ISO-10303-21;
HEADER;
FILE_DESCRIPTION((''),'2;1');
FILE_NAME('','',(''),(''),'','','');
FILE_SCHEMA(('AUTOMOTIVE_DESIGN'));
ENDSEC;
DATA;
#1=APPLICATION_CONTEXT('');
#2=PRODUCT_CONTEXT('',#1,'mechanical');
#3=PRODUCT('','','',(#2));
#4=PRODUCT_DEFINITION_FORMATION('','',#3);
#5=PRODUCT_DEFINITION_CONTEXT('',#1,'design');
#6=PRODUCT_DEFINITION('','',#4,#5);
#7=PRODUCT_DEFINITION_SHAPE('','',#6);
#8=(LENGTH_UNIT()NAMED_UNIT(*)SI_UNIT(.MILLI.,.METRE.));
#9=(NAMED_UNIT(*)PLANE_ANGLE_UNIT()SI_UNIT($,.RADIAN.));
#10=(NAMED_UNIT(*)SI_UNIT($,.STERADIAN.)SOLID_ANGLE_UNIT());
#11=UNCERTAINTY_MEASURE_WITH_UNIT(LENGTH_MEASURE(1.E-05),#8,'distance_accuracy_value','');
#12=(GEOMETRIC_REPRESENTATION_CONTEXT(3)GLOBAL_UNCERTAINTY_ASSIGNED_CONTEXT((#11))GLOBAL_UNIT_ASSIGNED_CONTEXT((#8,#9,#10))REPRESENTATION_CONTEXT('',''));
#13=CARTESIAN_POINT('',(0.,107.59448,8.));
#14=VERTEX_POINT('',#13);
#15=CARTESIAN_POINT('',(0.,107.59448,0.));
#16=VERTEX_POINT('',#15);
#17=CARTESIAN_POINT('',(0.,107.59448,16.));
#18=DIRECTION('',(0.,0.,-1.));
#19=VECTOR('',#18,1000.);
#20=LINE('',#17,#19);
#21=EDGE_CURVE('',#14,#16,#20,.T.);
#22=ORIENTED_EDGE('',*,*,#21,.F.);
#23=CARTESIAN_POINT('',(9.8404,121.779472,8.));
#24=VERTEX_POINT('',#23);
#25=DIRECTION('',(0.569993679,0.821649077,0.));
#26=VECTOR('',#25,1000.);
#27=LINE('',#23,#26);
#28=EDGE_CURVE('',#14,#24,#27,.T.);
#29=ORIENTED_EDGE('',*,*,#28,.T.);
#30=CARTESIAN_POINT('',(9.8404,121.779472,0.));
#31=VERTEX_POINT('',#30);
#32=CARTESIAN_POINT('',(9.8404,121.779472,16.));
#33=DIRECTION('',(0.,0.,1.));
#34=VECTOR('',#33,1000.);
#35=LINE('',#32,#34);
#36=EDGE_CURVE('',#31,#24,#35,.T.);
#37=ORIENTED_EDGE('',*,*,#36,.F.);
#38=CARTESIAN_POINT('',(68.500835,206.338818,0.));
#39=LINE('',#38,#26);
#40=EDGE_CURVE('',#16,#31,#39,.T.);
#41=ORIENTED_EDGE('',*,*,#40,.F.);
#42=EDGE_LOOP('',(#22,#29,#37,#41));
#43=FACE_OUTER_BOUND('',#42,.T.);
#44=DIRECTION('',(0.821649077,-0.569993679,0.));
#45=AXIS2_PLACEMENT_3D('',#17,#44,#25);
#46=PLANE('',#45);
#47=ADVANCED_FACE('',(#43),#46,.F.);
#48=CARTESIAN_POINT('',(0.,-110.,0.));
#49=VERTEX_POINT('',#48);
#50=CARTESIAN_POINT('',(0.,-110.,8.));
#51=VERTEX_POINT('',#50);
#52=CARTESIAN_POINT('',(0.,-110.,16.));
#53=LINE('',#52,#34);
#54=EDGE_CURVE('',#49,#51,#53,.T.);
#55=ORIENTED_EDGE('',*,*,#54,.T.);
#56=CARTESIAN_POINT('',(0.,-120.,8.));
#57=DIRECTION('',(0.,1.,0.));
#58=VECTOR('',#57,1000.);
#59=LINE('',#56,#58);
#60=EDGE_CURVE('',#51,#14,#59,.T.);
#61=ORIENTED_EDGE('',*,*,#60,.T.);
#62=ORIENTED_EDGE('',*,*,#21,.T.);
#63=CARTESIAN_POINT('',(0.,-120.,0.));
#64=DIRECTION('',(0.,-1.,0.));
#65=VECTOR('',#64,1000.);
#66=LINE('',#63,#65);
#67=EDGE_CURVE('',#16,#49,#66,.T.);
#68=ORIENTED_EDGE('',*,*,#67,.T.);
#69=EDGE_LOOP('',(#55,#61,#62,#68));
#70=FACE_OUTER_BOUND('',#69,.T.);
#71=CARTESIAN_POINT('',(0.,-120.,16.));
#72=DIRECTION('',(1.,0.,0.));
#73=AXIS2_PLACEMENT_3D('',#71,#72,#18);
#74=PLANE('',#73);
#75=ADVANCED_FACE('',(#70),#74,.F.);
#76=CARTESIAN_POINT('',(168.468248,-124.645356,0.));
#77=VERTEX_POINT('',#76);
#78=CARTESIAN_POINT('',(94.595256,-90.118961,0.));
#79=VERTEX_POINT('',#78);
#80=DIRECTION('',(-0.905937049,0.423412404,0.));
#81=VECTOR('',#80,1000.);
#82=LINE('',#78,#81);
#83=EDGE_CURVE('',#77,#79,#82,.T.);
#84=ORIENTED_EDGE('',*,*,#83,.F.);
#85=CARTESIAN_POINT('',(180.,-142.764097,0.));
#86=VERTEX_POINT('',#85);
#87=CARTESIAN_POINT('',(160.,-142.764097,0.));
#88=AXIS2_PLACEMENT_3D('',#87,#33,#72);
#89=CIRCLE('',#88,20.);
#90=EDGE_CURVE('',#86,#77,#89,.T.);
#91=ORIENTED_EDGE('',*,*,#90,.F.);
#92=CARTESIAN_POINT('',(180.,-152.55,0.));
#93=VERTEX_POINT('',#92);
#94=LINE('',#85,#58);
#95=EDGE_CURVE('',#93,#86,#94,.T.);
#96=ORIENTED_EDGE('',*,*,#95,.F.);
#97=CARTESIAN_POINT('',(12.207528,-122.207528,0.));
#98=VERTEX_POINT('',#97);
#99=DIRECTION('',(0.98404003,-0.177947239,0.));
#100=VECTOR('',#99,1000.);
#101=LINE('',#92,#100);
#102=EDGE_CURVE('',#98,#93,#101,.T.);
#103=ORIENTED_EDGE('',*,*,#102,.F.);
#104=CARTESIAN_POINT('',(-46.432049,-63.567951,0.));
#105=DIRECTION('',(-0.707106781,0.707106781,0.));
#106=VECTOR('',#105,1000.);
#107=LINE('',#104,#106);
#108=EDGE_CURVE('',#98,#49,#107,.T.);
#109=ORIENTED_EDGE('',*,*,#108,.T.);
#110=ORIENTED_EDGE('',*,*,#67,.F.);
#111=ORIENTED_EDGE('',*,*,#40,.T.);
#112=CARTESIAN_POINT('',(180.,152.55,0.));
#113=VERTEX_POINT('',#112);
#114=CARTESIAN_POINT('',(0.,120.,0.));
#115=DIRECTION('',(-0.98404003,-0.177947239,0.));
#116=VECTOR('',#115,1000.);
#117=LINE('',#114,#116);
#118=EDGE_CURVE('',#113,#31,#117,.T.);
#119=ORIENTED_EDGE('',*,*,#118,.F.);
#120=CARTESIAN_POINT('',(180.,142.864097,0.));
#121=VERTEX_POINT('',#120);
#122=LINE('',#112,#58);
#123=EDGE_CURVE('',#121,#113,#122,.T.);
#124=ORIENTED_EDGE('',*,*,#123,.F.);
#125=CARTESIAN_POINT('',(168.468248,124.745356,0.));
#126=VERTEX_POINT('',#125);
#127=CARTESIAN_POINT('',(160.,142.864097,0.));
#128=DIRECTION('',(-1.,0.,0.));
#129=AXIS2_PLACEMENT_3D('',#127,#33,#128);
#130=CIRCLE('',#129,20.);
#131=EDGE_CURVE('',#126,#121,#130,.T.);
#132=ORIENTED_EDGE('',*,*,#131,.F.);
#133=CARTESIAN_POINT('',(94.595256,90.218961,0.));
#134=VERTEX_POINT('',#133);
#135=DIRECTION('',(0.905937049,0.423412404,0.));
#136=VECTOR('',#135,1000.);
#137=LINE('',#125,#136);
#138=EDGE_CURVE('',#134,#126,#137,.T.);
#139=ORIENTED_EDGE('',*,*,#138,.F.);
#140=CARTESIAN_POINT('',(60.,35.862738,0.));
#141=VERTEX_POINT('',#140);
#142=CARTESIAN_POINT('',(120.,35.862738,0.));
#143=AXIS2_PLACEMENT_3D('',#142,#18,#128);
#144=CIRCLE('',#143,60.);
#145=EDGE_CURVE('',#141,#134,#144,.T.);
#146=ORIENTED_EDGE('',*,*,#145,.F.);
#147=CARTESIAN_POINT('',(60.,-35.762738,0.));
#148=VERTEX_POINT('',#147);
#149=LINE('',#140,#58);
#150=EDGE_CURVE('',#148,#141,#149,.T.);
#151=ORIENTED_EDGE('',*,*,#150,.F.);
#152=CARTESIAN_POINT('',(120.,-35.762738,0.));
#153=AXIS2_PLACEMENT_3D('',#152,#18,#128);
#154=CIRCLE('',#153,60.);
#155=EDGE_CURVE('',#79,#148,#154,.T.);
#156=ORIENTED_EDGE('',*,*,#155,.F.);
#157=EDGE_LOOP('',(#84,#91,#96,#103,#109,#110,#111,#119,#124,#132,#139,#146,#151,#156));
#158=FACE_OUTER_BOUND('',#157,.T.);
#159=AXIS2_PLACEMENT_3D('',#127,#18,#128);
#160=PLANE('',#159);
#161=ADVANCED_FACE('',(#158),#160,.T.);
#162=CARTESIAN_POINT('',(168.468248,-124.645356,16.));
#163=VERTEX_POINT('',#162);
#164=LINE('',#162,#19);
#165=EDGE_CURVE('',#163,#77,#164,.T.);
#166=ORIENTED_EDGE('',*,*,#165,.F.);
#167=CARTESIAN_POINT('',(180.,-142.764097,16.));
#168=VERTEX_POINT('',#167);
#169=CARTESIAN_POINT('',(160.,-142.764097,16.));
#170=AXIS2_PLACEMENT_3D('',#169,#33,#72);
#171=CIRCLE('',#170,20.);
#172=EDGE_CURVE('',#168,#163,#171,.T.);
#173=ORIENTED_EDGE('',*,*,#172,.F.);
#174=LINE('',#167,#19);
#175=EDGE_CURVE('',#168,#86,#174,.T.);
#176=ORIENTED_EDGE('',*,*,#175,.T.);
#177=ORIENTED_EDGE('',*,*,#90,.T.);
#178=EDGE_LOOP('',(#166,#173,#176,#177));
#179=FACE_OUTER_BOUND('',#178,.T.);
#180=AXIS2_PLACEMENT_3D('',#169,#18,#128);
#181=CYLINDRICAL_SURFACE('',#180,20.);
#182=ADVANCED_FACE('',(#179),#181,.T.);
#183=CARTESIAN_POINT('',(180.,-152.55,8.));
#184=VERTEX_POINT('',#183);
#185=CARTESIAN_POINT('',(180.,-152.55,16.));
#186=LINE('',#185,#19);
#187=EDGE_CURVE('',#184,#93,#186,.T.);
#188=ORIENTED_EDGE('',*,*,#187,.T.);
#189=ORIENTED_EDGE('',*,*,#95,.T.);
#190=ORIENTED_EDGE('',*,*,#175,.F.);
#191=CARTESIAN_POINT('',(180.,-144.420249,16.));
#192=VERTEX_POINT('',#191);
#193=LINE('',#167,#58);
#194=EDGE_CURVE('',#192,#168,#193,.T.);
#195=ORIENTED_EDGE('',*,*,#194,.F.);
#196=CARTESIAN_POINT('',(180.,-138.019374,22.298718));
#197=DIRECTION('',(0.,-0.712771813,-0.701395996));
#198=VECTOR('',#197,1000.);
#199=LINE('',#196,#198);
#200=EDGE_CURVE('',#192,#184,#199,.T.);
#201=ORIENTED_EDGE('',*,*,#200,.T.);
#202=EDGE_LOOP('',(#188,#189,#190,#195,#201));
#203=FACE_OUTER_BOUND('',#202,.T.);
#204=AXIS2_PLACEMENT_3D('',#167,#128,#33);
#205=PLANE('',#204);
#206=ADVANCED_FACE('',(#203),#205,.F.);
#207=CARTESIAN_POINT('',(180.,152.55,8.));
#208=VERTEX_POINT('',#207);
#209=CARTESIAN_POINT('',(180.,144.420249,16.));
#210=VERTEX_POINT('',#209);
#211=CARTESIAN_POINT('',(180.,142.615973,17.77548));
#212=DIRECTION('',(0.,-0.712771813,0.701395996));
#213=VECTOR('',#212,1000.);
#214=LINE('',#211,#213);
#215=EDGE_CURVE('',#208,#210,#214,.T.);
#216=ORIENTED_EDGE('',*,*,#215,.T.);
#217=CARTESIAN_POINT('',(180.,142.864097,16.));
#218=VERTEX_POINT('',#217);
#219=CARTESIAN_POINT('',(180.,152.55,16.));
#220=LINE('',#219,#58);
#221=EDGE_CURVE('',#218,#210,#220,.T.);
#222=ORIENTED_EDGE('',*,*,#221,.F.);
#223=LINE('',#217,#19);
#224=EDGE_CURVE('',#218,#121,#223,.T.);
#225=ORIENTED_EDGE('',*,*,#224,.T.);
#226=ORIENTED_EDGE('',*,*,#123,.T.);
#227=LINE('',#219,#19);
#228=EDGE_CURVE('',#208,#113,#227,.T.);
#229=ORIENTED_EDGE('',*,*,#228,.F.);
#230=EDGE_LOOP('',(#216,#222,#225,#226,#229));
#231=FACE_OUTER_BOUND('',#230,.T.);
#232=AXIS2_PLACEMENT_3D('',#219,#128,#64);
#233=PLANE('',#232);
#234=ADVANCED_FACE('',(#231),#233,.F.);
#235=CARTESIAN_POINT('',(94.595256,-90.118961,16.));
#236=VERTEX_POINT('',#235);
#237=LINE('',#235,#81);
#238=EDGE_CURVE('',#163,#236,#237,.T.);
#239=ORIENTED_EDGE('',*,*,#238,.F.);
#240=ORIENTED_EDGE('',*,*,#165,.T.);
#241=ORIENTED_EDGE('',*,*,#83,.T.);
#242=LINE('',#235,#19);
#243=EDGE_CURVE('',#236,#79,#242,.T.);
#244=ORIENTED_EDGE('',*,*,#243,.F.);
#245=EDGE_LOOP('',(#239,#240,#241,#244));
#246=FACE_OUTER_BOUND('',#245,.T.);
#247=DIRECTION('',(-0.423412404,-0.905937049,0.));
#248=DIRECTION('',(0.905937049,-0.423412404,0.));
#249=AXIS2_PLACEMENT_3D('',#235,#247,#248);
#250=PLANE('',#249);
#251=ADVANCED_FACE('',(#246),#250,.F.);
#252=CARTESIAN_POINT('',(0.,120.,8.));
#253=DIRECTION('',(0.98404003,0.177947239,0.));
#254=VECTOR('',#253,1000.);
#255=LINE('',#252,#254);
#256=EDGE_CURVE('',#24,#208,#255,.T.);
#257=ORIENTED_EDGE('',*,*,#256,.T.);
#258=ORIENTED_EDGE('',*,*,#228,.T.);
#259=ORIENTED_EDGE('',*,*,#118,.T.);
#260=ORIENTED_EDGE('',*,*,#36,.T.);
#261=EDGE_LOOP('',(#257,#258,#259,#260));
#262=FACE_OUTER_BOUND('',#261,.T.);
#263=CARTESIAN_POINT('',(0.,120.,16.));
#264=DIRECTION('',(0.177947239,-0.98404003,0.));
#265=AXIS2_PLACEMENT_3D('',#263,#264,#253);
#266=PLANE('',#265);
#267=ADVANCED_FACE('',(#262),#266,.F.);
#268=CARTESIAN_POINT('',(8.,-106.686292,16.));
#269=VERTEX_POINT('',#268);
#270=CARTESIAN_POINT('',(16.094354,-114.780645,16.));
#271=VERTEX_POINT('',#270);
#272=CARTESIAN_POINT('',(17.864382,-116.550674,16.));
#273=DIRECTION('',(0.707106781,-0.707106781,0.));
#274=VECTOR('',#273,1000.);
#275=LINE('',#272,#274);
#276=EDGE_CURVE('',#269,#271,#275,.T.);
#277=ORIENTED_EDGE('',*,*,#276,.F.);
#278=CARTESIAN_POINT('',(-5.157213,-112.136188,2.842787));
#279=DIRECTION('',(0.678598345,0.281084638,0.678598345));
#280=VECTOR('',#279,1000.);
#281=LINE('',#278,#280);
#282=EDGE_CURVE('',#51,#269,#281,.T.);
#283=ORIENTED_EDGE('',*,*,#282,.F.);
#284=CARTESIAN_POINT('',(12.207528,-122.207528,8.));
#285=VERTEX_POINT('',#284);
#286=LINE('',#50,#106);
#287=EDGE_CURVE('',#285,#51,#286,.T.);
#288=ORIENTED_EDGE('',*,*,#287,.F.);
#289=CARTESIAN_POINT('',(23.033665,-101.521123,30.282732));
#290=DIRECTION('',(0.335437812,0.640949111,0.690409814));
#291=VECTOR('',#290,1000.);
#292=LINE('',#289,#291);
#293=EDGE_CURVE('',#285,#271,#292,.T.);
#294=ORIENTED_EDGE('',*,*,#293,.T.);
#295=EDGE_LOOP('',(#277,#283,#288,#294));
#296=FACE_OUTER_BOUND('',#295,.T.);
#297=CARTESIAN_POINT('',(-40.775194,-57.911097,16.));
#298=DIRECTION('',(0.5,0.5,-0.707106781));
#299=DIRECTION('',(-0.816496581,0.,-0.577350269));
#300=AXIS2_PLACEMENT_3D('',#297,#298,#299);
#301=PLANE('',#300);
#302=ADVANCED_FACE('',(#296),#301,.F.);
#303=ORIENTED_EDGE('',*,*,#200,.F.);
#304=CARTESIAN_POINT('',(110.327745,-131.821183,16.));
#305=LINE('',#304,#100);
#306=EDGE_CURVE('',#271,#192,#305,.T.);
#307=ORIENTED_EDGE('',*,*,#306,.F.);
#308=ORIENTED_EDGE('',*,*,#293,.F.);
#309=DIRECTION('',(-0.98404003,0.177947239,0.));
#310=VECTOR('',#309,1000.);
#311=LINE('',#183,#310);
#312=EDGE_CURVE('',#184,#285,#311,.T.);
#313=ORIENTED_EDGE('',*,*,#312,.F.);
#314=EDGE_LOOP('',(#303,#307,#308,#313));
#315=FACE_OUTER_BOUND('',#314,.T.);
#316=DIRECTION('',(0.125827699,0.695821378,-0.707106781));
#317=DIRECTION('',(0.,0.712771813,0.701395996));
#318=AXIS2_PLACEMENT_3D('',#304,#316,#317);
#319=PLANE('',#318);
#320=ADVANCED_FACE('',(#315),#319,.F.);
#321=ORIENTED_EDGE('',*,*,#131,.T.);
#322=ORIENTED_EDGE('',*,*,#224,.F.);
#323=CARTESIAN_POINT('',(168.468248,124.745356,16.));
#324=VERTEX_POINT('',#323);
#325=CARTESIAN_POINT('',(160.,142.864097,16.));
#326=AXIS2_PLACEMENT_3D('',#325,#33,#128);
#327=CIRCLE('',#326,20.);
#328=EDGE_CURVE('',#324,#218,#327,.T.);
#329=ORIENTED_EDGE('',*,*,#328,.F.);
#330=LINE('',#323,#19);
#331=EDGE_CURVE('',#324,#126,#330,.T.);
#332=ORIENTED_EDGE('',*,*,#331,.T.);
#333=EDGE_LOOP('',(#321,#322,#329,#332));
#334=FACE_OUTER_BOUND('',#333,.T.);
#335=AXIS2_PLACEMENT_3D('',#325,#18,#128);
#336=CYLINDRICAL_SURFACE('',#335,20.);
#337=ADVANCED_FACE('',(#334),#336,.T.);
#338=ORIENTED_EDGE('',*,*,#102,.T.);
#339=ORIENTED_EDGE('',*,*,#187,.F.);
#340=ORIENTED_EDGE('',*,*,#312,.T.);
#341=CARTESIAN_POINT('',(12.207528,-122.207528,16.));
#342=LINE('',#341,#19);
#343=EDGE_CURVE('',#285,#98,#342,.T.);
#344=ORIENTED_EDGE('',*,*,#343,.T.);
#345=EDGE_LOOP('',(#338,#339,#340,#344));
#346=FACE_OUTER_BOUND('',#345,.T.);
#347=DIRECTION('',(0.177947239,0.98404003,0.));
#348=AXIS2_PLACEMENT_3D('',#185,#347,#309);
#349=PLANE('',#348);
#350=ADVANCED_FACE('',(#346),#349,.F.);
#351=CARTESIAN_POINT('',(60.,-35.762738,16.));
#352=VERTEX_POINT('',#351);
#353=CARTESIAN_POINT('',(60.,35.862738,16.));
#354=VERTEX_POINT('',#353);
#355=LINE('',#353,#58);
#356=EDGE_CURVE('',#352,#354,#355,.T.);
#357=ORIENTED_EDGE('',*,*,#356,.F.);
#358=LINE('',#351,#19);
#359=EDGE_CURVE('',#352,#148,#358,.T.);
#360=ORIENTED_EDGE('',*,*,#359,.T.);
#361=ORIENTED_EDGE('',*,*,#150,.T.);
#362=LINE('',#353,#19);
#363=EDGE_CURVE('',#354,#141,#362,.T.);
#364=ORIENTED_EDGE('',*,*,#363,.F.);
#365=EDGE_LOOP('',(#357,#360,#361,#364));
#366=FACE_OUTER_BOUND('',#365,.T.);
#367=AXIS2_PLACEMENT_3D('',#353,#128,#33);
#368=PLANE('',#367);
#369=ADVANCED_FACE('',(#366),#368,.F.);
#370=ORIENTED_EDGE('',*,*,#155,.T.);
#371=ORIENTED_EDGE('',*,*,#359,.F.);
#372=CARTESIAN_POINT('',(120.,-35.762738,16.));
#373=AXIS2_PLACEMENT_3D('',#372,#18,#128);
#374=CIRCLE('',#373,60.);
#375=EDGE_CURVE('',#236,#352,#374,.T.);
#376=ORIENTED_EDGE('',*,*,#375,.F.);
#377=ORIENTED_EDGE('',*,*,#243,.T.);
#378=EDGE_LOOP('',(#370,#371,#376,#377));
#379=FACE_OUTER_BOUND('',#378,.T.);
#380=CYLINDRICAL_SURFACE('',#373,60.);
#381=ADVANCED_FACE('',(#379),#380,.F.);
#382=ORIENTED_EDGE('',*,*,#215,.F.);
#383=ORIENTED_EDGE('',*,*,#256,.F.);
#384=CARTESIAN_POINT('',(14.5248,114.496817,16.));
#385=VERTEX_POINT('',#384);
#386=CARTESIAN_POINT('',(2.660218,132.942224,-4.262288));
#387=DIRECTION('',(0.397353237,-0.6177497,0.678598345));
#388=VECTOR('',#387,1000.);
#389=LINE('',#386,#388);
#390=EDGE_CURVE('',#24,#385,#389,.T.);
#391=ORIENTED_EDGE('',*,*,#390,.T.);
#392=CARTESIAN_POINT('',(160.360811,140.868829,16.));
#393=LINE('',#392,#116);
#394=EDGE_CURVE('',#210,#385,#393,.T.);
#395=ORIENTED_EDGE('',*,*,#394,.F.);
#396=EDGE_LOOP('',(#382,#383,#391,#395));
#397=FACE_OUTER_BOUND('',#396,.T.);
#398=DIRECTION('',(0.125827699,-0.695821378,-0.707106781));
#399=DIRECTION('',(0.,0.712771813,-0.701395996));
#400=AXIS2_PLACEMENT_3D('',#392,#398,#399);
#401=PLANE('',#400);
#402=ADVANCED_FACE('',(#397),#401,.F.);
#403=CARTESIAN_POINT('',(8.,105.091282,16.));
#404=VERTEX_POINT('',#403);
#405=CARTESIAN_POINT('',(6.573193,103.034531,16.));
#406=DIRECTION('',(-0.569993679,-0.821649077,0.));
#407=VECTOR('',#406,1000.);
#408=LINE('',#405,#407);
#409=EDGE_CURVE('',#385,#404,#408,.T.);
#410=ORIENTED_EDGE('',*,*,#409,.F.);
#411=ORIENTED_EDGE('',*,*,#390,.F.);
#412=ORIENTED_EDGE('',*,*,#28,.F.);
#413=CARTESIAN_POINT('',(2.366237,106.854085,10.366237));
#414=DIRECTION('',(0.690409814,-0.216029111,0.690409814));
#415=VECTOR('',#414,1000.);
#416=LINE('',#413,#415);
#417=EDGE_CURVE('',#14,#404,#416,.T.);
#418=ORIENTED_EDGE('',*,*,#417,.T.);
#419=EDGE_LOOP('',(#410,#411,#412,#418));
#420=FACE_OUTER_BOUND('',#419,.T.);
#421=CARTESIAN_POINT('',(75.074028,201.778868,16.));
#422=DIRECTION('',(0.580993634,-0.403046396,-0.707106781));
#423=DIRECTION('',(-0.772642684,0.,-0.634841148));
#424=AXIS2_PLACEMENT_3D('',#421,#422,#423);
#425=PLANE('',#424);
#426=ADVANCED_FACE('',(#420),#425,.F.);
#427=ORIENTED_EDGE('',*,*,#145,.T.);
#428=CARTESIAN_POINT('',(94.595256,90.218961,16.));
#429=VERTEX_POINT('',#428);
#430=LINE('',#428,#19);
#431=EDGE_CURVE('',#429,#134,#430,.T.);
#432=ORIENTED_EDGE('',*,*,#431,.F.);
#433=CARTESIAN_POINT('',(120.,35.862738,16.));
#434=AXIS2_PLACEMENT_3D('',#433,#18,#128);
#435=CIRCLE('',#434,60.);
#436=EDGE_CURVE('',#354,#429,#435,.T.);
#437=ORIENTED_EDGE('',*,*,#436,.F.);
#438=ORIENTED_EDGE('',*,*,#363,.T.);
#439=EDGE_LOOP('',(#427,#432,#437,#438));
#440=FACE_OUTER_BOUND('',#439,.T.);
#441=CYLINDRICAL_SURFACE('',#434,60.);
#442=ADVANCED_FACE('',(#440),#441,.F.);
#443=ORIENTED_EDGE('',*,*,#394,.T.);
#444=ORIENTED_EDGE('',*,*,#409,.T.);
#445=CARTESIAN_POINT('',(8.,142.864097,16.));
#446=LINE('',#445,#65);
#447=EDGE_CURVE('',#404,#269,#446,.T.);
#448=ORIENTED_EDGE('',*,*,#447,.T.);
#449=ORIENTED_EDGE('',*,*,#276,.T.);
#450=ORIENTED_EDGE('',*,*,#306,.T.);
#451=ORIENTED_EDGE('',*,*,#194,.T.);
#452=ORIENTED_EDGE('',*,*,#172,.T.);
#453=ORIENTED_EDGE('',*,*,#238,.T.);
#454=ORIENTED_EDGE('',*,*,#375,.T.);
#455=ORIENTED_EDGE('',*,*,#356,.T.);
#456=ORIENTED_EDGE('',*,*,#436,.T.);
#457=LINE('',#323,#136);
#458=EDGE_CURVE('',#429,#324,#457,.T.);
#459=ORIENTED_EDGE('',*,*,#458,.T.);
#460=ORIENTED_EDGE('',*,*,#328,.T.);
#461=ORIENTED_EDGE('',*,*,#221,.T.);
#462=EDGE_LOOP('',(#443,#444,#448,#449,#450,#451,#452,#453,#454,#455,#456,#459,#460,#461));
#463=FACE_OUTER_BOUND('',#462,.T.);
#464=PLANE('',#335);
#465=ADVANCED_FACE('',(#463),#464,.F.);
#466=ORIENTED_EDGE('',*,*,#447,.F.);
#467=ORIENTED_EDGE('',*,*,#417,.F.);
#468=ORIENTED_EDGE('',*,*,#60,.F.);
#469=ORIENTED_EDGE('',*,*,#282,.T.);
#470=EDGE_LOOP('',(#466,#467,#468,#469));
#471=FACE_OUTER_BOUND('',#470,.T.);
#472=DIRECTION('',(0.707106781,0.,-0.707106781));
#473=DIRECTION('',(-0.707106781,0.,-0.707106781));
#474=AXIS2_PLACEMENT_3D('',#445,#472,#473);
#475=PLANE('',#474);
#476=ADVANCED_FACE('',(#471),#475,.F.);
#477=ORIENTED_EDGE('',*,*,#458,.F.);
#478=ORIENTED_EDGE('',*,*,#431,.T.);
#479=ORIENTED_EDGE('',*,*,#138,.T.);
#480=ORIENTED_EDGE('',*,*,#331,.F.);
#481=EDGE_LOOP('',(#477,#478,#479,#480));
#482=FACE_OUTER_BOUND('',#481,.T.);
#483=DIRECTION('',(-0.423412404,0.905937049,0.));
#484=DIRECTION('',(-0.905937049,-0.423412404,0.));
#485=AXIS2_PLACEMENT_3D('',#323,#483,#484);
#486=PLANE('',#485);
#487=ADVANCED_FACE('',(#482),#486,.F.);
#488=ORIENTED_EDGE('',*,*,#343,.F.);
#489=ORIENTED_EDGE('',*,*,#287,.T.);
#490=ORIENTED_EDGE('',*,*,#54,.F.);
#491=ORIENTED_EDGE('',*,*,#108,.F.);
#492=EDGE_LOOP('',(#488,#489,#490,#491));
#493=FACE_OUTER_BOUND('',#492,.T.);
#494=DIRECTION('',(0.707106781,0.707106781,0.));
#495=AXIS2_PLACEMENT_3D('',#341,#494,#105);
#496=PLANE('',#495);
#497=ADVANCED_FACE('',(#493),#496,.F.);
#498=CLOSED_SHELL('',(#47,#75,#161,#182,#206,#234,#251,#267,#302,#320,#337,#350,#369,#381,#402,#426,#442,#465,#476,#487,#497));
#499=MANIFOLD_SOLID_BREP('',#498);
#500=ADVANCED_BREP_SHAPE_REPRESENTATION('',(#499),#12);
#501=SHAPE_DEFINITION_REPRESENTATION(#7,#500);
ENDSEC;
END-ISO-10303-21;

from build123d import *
from OCP.BRepFilletAPI import BRepFilletAPI_MakeChamfer

# Parameters (mm, degrees)
BOSS_EXTRUDE1_DEPTH = 16
CHAMFER1_SIZE       = 10
CHAMFER1_SIZE2      = 12.4055197
CHAMFER2_SIZE       = 8


with BuildPart() as part:
    # Sketch1 → Boss-Extrude1 (new body)
    with BuildSketch(Plane.XY):
        with BuildLine():
            Line((0, -120), (0, 120))
            Line((0, 120), (180, 152.55))
            Line((180, 152.55), (180, 142.864097444))
            ThreePointArc((180, 142.864097444), (176.872536286, 132.125497941), (168.468248072, 124.745356467))
            Line((168.468248072, 124.745356467), (94.595255785, 90.218960551))
            ThreePointArc((94.595255785, 90.218960551), (69.382391143, 68.078536128), (60, 35.862737619))
            Line((60, 35.862737619), (60, -35.762737619))
            ThreePointArc((60, -35.762737619), (69.382391143, -67.978536128), (94.595255785, -90.118960551))
            Line((94.595255785, -90.118960551), (168.468248072, -124.645356467))
            ThreePointArc((168.468248072, -124.645356467), (176.872536286, -132.025497941), (180, -142.764097444))
            Line((180, -142.764097444), (180, -152.55))
            Line((180, -152.55), (0, -120))
        make_face()
    extrude(amount=BOSS_EXTRUDE1_DEPTH)

    # Chamfer1: one chamfer whose edges measure the first distance from different faces: ONE call of the kernel's chamfer builder (chamfer() names one face for all edges)
    chamfer1_edges_1 = [part.edges().sort_by_distance(p)[0] for p in [
        (0, -120, 8),
    ]]
    chamfer1_side_1 = [part.faces().sort_by_distance(p)[0] for p in [
        (0, 0, 8),
    ]]
    chamfer1_edges_2 = [part.edges().sort_by_distance(p)[0] for p in [
        (0, 120, 8),
    ]]
    chamfer1_side_2 = [part.faces().sort_by_distance(p)[0] for p in [
        (90, 136.275, 8),
    ]]
    chamfer1 = BRepFilletAPI_MakeChamfer(part.part.solid().wrapped)
    for e in chamfer1_edges_1:
        chamfer1.Add(CHAMFER1_SIZE, CHAMFER1_SIZE2, e.wrapped, chamfer1_side_1[0].wrapped)  # the first distance lies on this face
    for e in chamfer1_edges_2:
        chamfer1.Add(CHAMFER1_SIZE, CHAMFER1_SIZE2, e.wrapped, chamfer1_side_2[0].wrapped)  # the first distance lies on this face
    add(Compound.cast(chamfer1.Shape()), mode=Mode.REPLACE)

    # Chamfer2
    chamfer2_edges = [part.edges().sort_by_distance(p)[0] for p in [
        (0, -1.20275985, 16),
        (96.103763988, -137.378763988, 16),
        (6.103763988, -116.103763988, 16),
        (4.920200149, 114.686976343, 16),
        (94.920200149, 137.164736194, 16),
    ]]
    chamfer(chamfer2_edges, length=CHAMFER2_SIZE)


solid = part.part
